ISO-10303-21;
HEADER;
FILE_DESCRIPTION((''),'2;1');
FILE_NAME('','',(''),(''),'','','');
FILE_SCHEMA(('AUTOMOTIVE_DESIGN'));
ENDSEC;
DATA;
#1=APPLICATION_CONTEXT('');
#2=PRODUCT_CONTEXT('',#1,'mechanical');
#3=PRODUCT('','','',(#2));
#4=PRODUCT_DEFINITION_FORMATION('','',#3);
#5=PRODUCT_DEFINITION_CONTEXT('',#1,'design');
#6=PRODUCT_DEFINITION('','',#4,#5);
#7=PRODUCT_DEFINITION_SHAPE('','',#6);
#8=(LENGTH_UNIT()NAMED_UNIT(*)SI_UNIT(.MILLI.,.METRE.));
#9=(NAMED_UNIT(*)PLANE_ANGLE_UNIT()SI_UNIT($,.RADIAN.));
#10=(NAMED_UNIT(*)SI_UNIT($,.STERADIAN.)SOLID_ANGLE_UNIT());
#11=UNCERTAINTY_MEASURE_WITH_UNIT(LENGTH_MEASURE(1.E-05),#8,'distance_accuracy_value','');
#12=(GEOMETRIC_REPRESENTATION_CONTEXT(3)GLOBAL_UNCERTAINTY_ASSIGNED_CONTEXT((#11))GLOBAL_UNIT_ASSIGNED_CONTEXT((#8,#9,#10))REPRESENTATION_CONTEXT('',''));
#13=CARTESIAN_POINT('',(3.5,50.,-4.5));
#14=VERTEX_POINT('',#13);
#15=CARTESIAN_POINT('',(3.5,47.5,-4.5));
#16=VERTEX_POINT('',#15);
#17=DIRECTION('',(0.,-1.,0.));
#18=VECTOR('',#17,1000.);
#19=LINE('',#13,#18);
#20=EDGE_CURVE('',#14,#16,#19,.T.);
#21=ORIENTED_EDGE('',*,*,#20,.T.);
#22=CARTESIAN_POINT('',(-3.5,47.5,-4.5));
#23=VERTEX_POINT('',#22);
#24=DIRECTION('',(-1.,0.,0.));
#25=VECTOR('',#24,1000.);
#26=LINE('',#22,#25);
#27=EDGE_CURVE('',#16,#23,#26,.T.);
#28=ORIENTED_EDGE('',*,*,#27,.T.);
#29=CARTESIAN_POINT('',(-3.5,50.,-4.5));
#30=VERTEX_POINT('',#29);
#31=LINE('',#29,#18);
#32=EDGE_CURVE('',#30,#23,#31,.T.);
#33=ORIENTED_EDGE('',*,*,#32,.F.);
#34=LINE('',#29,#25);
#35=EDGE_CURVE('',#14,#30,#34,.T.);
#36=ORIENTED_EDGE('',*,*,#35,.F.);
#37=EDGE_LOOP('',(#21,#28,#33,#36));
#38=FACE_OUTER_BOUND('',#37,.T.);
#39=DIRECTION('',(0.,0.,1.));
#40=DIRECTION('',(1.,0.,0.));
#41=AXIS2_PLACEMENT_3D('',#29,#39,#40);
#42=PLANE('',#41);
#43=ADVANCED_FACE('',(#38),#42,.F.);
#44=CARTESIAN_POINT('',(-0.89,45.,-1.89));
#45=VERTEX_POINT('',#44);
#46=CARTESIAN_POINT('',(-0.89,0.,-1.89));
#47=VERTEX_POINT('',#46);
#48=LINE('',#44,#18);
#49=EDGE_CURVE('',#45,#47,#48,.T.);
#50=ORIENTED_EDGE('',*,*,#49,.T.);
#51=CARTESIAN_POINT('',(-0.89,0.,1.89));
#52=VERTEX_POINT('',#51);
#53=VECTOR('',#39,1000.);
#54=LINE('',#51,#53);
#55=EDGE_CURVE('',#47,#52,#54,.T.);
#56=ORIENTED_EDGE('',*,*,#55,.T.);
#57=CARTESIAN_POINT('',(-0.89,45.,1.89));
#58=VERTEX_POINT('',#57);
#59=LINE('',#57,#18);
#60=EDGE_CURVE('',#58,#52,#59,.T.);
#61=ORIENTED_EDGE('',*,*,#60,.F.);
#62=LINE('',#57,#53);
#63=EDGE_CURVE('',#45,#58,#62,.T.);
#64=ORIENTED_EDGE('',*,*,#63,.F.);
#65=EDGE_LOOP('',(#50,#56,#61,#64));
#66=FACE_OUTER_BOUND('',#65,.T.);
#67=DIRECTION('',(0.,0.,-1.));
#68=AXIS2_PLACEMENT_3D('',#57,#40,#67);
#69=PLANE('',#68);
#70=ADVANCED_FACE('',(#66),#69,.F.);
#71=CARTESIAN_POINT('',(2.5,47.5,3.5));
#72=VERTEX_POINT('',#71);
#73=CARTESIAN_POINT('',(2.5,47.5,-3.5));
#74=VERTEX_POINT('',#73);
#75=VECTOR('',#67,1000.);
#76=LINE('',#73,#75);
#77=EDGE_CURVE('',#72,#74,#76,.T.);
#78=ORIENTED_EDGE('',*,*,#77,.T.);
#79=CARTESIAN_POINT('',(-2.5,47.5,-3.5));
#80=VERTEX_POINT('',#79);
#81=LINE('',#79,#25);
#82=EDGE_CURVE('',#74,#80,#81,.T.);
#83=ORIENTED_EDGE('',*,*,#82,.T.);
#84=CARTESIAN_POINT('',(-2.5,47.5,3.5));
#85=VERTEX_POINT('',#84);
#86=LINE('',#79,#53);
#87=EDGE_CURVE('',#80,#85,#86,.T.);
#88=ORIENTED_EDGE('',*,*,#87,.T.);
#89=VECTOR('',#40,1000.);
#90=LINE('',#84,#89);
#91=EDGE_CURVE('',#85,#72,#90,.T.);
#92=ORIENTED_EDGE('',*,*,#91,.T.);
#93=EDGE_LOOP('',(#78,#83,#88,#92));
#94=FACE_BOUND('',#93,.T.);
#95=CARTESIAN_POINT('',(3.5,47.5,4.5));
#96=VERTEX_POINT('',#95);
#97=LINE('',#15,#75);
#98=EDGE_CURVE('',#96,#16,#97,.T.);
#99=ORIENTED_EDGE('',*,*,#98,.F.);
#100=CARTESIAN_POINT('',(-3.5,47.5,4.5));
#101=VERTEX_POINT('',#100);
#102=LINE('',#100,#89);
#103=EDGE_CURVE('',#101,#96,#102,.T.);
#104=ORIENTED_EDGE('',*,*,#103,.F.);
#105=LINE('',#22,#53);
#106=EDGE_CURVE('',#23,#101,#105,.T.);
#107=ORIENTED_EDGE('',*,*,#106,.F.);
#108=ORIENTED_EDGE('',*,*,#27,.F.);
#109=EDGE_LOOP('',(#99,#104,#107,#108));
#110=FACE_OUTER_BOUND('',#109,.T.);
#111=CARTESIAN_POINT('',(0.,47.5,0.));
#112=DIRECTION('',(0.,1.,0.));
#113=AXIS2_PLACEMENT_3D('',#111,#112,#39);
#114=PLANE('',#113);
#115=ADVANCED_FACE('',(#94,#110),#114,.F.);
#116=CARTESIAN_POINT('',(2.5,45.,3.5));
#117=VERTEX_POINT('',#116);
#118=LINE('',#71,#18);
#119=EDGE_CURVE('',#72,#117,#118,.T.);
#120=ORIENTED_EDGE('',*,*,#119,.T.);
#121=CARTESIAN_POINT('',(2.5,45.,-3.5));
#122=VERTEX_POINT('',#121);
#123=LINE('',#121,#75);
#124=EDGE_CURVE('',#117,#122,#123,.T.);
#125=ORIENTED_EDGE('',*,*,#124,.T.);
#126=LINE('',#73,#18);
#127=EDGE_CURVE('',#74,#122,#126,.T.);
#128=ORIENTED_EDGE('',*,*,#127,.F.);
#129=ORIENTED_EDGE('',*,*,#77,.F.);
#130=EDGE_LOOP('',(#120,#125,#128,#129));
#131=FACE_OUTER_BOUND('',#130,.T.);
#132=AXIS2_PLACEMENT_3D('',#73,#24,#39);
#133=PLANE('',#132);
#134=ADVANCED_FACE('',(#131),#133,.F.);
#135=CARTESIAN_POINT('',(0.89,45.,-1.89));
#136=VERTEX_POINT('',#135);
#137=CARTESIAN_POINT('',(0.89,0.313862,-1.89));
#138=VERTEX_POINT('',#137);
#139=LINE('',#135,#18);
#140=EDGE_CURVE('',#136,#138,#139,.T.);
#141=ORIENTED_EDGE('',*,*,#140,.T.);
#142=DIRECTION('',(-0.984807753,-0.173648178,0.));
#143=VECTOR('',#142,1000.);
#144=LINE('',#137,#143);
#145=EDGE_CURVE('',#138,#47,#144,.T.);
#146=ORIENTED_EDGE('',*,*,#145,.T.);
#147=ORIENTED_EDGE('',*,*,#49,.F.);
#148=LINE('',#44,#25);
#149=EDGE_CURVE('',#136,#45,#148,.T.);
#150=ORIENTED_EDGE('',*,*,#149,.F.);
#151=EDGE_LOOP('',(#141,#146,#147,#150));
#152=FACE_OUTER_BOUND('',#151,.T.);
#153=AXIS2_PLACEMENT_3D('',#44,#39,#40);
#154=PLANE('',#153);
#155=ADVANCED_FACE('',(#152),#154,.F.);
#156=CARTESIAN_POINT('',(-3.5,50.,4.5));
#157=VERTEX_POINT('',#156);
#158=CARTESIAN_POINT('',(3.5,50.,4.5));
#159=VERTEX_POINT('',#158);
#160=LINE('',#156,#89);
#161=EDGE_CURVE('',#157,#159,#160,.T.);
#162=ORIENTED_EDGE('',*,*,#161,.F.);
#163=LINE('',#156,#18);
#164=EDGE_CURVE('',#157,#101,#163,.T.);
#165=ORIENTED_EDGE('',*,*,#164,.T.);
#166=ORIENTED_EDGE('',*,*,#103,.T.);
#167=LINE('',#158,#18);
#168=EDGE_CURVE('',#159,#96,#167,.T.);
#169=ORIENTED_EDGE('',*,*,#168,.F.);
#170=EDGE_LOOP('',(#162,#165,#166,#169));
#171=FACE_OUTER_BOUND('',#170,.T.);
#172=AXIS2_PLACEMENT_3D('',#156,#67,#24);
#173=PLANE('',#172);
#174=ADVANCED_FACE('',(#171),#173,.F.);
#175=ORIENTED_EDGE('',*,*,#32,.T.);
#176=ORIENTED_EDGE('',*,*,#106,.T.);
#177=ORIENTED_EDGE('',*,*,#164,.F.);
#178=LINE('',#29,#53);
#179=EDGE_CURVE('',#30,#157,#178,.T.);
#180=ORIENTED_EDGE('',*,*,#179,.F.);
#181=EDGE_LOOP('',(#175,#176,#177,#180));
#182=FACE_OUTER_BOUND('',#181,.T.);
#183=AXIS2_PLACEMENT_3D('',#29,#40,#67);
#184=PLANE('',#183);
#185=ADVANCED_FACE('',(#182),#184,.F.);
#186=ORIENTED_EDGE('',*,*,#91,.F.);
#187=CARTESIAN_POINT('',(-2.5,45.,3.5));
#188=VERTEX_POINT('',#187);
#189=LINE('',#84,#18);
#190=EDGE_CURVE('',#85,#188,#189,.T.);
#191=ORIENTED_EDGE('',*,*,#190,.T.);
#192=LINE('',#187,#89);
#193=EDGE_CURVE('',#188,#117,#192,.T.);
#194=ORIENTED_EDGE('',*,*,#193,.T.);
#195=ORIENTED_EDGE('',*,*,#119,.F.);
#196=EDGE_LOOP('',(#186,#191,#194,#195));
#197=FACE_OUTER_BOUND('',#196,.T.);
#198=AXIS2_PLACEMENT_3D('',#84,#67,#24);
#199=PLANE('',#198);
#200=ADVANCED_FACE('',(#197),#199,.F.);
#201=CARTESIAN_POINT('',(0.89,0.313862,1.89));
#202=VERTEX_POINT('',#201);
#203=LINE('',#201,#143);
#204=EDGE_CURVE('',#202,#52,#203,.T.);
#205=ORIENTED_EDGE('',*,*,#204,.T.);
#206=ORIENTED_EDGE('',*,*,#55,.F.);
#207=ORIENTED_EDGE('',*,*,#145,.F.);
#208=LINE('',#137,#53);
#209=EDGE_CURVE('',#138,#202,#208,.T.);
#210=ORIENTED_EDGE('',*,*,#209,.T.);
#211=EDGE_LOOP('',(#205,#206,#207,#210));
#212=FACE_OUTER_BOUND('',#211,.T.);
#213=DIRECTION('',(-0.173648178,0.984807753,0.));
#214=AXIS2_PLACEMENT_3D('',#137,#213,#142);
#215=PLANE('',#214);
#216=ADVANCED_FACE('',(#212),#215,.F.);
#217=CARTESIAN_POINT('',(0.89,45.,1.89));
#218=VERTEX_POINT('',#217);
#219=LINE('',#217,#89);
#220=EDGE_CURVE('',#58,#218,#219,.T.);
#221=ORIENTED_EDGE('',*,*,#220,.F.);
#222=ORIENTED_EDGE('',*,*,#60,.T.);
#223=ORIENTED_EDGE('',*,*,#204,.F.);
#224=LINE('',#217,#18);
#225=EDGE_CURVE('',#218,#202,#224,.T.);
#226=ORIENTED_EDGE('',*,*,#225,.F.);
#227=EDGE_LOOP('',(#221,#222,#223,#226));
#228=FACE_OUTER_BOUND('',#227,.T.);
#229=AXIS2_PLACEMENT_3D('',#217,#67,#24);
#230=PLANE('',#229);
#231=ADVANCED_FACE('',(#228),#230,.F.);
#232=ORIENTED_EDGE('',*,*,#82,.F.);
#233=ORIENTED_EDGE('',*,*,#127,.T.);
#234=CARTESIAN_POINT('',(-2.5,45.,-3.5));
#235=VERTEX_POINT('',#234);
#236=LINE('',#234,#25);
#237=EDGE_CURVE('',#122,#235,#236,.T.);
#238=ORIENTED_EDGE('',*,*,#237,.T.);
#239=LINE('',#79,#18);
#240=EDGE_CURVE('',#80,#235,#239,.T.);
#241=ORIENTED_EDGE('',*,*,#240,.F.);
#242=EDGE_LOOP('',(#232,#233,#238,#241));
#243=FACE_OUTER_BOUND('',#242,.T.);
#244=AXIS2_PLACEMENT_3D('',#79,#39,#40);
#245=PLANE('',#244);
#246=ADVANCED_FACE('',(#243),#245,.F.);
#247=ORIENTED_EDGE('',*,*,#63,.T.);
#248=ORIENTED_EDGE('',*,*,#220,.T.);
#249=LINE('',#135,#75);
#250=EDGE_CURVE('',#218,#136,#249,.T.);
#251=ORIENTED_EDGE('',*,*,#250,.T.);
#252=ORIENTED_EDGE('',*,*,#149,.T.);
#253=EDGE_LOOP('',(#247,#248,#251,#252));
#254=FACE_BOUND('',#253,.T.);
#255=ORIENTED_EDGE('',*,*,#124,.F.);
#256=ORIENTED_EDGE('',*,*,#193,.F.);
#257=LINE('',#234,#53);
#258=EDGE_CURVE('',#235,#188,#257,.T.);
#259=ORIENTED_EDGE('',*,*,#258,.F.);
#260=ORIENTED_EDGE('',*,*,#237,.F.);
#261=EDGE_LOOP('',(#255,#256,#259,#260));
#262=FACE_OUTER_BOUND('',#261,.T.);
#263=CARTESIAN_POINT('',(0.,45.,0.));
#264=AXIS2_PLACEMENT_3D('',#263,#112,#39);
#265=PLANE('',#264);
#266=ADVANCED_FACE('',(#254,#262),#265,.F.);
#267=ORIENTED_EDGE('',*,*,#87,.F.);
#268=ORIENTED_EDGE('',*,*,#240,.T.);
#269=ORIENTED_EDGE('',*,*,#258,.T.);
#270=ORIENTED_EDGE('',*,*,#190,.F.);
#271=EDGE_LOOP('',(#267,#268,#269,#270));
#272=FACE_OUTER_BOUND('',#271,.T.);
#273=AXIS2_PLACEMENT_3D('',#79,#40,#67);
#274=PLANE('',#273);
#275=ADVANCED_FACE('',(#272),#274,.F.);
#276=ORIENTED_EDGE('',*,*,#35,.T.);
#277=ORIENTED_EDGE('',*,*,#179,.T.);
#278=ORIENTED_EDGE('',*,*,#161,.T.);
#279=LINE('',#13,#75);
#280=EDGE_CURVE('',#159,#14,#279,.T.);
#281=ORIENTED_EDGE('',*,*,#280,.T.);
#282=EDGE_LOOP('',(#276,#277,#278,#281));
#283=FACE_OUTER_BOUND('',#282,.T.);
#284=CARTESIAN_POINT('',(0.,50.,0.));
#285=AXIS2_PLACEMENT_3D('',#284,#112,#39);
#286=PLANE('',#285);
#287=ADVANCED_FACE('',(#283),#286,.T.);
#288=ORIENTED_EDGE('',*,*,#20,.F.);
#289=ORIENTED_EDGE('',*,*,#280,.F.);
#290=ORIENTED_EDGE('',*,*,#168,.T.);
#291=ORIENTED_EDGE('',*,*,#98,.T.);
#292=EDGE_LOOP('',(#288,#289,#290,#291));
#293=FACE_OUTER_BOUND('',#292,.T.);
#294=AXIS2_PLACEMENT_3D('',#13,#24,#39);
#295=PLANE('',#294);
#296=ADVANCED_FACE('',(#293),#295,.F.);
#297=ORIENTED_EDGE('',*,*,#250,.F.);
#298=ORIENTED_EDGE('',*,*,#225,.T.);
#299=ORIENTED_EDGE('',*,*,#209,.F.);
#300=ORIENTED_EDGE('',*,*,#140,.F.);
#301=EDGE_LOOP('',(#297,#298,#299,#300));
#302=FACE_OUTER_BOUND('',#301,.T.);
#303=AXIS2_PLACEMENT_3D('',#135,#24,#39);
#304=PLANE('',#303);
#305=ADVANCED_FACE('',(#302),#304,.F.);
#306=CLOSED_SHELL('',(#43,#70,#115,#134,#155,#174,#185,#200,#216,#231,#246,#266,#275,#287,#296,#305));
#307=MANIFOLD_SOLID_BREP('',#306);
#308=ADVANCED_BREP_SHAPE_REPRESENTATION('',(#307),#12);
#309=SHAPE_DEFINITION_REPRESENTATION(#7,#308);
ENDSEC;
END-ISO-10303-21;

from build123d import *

# Parameters (mm, degrees)
SKETCH1_W           = 1.78
SKETCH1_H           = 3.78
BOSS_EXTRUDE1_DEPTH = 45
CUT_EXTRUDE1_DEPTH  = 46.167250304
SKETCH3_W           = 5
SKETCH3_H           = 7
BOSS_EXTRUDE2_DEPTH = 2.5
SKETCH4_W           = 7
SKETCH4_H           = 9
BOSS_EXTRUDE3_DEPTH = 2.5


with BuildPart() as part:
    # Sketch1 → Boss-Extrude1 (new body)
    with BuildSketch(Plane(origin=(0, 0, 0), x_dir=(1, 0, 0), z_dir=(0, 1, 0))):
        Rectangle(SKETCH1_W, SKETCH1_H)
    extrude(amount=BOSS_EXTRUDE1_DEPTH)

    # Sketch2 → Cut-Extrude1 (cut, through all)
    with BuildSketch(Plane.XY.offset(1.89)):
        Polygon((-0.89, 0), (0.89, 0), (0.89, 0.313862026), align=None)
    extrude(amount=-CUT_EXTRUDE1_DEPTH, mode=Mode.SUBTRACT)

    # Sketch3 → Boss-Extrude2 (add)
    with BuildSketch(Plane(origin=(0, 45, 0), x_dir=(1, 0, 0), z_dir=(0, 1, 0))):
        Rectangle(SKETCH3_W, SKETCH3_H)
    extrude(amount=BOSS_EXTRUDE2_DEPTH)

    # Sketch4 → Boss-Extrude3 (add)
    with BuildSketch(Plane(origin=(0, 47.5, 0), x_dir=(1, 0, 0), z_dir=(0, 1, 0))):
        Rectangle(SKETCH4_W, SKETCH4_H)
    extrude(amount=BOSS_EXTRUDE3_DEPTH)


solid = part.part
